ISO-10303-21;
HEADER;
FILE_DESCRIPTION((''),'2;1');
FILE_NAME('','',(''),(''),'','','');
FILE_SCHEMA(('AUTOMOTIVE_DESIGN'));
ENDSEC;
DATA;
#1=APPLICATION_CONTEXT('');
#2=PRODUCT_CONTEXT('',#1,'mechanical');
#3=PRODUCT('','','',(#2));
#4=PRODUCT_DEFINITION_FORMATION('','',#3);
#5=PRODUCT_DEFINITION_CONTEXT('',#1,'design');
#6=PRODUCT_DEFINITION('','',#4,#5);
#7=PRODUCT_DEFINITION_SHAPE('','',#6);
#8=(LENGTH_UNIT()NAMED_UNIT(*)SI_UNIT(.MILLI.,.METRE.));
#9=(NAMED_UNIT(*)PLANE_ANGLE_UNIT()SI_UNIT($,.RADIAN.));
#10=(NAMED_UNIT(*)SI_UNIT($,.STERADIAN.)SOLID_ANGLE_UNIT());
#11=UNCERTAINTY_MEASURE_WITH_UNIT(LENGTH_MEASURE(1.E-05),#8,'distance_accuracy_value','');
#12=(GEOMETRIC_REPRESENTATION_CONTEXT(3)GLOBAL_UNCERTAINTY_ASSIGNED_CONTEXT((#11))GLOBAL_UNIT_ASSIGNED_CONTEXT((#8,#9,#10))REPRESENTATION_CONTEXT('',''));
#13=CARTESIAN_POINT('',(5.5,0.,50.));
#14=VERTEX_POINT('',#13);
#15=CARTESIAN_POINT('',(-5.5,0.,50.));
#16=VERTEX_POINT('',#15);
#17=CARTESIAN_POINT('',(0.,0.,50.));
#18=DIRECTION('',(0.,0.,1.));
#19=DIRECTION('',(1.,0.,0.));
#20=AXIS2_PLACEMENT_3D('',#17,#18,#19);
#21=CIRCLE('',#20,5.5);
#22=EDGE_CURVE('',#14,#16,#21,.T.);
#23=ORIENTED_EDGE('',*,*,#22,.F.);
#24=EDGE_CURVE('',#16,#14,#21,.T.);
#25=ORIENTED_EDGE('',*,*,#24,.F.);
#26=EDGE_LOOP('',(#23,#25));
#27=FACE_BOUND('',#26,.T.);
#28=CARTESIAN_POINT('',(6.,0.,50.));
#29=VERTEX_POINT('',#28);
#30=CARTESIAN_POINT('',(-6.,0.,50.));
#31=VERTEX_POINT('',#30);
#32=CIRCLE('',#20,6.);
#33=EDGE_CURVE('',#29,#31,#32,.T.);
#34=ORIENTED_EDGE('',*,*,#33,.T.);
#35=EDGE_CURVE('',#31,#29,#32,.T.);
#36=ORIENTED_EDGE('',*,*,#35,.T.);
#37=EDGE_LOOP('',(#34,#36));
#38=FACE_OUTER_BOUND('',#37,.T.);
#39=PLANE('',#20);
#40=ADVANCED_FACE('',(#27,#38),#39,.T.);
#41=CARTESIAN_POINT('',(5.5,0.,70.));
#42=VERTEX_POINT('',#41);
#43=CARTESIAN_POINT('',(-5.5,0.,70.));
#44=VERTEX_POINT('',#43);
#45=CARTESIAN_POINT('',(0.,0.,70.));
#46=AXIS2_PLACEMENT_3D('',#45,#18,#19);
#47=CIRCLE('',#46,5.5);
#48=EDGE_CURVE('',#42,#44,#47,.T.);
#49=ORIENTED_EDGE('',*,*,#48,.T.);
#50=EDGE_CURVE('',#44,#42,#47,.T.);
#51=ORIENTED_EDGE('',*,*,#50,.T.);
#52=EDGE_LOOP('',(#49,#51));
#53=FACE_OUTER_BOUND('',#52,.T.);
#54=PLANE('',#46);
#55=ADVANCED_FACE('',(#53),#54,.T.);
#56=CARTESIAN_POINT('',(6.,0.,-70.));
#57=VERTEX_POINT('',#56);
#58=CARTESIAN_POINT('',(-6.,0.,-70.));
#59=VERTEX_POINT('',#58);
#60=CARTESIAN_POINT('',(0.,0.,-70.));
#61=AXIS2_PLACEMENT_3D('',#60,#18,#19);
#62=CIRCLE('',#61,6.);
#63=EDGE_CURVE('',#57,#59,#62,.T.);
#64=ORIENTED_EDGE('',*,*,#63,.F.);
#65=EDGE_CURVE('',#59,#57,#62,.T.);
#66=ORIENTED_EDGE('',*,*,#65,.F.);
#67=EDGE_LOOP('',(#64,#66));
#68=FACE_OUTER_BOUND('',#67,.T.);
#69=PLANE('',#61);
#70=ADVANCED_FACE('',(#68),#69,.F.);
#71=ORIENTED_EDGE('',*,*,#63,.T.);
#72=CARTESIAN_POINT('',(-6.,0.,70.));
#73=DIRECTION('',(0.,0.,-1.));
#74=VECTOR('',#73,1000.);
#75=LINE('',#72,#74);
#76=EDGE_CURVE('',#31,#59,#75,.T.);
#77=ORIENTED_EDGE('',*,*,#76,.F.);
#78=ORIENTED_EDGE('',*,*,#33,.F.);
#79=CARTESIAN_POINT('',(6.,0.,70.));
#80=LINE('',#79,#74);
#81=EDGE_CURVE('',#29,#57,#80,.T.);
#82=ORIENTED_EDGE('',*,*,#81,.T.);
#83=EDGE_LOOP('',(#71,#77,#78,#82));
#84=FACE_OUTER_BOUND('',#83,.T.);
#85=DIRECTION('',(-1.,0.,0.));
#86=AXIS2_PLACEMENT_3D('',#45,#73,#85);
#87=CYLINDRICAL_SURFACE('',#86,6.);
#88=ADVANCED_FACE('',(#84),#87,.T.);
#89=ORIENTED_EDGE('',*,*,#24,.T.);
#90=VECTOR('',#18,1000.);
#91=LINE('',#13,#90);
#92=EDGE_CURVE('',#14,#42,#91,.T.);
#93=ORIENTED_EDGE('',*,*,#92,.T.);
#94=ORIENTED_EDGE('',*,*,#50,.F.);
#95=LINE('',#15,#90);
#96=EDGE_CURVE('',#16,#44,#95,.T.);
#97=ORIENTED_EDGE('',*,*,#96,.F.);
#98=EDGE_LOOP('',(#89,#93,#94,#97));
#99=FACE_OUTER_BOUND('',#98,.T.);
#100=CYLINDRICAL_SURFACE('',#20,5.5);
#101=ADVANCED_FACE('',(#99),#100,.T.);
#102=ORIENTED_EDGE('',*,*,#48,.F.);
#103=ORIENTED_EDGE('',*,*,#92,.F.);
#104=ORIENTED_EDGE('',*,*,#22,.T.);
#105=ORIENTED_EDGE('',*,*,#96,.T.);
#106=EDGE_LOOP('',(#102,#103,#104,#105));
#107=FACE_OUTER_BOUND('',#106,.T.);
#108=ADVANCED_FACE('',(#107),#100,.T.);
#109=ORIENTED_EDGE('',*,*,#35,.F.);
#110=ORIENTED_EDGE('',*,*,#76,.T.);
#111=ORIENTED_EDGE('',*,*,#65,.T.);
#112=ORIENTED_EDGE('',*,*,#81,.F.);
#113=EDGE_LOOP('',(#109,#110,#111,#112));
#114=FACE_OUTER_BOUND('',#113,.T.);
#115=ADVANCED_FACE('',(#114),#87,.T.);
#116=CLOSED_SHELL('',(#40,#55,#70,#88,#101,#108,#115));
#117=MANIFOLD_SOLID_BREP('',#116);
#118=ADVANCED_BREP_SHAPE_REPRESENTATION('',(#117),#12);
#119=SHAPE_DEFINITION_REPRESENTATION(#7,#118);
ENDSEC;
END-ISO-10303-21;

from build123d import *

# Parameters (mm, degrees)
SKETCH_1_R          = 6
EXTRUDE_3_DEPTH     = 70
SKETCH_3_R          = 6
SKETCH_3_R_2        = 5.5
CUT_EXTRUDE_1_DEPTH = 20


with BuildPart() as part:
    # 草图1 → 凸台-拉伸3 (new, symmetric)
    with BuildSketch(Plane.XY):
        Circle(SKETCH_1_R)
    extrude(amount=EXTRUDE_3_DEPTH, both=True)

    # 草图3 → 切除-拉伸1 (cut)
    with BuildSketch(Plane.XY.offset(70)):
        Circle(SKETCH_3_R)
        Circle(SKETCH_3_R_2, mode=Mode.SUBTRACT)
    extrude(amount=-CUT_EXTRUDE_1_DEPTH, mode=Mode.SUBTRACT)


solid = part.part
